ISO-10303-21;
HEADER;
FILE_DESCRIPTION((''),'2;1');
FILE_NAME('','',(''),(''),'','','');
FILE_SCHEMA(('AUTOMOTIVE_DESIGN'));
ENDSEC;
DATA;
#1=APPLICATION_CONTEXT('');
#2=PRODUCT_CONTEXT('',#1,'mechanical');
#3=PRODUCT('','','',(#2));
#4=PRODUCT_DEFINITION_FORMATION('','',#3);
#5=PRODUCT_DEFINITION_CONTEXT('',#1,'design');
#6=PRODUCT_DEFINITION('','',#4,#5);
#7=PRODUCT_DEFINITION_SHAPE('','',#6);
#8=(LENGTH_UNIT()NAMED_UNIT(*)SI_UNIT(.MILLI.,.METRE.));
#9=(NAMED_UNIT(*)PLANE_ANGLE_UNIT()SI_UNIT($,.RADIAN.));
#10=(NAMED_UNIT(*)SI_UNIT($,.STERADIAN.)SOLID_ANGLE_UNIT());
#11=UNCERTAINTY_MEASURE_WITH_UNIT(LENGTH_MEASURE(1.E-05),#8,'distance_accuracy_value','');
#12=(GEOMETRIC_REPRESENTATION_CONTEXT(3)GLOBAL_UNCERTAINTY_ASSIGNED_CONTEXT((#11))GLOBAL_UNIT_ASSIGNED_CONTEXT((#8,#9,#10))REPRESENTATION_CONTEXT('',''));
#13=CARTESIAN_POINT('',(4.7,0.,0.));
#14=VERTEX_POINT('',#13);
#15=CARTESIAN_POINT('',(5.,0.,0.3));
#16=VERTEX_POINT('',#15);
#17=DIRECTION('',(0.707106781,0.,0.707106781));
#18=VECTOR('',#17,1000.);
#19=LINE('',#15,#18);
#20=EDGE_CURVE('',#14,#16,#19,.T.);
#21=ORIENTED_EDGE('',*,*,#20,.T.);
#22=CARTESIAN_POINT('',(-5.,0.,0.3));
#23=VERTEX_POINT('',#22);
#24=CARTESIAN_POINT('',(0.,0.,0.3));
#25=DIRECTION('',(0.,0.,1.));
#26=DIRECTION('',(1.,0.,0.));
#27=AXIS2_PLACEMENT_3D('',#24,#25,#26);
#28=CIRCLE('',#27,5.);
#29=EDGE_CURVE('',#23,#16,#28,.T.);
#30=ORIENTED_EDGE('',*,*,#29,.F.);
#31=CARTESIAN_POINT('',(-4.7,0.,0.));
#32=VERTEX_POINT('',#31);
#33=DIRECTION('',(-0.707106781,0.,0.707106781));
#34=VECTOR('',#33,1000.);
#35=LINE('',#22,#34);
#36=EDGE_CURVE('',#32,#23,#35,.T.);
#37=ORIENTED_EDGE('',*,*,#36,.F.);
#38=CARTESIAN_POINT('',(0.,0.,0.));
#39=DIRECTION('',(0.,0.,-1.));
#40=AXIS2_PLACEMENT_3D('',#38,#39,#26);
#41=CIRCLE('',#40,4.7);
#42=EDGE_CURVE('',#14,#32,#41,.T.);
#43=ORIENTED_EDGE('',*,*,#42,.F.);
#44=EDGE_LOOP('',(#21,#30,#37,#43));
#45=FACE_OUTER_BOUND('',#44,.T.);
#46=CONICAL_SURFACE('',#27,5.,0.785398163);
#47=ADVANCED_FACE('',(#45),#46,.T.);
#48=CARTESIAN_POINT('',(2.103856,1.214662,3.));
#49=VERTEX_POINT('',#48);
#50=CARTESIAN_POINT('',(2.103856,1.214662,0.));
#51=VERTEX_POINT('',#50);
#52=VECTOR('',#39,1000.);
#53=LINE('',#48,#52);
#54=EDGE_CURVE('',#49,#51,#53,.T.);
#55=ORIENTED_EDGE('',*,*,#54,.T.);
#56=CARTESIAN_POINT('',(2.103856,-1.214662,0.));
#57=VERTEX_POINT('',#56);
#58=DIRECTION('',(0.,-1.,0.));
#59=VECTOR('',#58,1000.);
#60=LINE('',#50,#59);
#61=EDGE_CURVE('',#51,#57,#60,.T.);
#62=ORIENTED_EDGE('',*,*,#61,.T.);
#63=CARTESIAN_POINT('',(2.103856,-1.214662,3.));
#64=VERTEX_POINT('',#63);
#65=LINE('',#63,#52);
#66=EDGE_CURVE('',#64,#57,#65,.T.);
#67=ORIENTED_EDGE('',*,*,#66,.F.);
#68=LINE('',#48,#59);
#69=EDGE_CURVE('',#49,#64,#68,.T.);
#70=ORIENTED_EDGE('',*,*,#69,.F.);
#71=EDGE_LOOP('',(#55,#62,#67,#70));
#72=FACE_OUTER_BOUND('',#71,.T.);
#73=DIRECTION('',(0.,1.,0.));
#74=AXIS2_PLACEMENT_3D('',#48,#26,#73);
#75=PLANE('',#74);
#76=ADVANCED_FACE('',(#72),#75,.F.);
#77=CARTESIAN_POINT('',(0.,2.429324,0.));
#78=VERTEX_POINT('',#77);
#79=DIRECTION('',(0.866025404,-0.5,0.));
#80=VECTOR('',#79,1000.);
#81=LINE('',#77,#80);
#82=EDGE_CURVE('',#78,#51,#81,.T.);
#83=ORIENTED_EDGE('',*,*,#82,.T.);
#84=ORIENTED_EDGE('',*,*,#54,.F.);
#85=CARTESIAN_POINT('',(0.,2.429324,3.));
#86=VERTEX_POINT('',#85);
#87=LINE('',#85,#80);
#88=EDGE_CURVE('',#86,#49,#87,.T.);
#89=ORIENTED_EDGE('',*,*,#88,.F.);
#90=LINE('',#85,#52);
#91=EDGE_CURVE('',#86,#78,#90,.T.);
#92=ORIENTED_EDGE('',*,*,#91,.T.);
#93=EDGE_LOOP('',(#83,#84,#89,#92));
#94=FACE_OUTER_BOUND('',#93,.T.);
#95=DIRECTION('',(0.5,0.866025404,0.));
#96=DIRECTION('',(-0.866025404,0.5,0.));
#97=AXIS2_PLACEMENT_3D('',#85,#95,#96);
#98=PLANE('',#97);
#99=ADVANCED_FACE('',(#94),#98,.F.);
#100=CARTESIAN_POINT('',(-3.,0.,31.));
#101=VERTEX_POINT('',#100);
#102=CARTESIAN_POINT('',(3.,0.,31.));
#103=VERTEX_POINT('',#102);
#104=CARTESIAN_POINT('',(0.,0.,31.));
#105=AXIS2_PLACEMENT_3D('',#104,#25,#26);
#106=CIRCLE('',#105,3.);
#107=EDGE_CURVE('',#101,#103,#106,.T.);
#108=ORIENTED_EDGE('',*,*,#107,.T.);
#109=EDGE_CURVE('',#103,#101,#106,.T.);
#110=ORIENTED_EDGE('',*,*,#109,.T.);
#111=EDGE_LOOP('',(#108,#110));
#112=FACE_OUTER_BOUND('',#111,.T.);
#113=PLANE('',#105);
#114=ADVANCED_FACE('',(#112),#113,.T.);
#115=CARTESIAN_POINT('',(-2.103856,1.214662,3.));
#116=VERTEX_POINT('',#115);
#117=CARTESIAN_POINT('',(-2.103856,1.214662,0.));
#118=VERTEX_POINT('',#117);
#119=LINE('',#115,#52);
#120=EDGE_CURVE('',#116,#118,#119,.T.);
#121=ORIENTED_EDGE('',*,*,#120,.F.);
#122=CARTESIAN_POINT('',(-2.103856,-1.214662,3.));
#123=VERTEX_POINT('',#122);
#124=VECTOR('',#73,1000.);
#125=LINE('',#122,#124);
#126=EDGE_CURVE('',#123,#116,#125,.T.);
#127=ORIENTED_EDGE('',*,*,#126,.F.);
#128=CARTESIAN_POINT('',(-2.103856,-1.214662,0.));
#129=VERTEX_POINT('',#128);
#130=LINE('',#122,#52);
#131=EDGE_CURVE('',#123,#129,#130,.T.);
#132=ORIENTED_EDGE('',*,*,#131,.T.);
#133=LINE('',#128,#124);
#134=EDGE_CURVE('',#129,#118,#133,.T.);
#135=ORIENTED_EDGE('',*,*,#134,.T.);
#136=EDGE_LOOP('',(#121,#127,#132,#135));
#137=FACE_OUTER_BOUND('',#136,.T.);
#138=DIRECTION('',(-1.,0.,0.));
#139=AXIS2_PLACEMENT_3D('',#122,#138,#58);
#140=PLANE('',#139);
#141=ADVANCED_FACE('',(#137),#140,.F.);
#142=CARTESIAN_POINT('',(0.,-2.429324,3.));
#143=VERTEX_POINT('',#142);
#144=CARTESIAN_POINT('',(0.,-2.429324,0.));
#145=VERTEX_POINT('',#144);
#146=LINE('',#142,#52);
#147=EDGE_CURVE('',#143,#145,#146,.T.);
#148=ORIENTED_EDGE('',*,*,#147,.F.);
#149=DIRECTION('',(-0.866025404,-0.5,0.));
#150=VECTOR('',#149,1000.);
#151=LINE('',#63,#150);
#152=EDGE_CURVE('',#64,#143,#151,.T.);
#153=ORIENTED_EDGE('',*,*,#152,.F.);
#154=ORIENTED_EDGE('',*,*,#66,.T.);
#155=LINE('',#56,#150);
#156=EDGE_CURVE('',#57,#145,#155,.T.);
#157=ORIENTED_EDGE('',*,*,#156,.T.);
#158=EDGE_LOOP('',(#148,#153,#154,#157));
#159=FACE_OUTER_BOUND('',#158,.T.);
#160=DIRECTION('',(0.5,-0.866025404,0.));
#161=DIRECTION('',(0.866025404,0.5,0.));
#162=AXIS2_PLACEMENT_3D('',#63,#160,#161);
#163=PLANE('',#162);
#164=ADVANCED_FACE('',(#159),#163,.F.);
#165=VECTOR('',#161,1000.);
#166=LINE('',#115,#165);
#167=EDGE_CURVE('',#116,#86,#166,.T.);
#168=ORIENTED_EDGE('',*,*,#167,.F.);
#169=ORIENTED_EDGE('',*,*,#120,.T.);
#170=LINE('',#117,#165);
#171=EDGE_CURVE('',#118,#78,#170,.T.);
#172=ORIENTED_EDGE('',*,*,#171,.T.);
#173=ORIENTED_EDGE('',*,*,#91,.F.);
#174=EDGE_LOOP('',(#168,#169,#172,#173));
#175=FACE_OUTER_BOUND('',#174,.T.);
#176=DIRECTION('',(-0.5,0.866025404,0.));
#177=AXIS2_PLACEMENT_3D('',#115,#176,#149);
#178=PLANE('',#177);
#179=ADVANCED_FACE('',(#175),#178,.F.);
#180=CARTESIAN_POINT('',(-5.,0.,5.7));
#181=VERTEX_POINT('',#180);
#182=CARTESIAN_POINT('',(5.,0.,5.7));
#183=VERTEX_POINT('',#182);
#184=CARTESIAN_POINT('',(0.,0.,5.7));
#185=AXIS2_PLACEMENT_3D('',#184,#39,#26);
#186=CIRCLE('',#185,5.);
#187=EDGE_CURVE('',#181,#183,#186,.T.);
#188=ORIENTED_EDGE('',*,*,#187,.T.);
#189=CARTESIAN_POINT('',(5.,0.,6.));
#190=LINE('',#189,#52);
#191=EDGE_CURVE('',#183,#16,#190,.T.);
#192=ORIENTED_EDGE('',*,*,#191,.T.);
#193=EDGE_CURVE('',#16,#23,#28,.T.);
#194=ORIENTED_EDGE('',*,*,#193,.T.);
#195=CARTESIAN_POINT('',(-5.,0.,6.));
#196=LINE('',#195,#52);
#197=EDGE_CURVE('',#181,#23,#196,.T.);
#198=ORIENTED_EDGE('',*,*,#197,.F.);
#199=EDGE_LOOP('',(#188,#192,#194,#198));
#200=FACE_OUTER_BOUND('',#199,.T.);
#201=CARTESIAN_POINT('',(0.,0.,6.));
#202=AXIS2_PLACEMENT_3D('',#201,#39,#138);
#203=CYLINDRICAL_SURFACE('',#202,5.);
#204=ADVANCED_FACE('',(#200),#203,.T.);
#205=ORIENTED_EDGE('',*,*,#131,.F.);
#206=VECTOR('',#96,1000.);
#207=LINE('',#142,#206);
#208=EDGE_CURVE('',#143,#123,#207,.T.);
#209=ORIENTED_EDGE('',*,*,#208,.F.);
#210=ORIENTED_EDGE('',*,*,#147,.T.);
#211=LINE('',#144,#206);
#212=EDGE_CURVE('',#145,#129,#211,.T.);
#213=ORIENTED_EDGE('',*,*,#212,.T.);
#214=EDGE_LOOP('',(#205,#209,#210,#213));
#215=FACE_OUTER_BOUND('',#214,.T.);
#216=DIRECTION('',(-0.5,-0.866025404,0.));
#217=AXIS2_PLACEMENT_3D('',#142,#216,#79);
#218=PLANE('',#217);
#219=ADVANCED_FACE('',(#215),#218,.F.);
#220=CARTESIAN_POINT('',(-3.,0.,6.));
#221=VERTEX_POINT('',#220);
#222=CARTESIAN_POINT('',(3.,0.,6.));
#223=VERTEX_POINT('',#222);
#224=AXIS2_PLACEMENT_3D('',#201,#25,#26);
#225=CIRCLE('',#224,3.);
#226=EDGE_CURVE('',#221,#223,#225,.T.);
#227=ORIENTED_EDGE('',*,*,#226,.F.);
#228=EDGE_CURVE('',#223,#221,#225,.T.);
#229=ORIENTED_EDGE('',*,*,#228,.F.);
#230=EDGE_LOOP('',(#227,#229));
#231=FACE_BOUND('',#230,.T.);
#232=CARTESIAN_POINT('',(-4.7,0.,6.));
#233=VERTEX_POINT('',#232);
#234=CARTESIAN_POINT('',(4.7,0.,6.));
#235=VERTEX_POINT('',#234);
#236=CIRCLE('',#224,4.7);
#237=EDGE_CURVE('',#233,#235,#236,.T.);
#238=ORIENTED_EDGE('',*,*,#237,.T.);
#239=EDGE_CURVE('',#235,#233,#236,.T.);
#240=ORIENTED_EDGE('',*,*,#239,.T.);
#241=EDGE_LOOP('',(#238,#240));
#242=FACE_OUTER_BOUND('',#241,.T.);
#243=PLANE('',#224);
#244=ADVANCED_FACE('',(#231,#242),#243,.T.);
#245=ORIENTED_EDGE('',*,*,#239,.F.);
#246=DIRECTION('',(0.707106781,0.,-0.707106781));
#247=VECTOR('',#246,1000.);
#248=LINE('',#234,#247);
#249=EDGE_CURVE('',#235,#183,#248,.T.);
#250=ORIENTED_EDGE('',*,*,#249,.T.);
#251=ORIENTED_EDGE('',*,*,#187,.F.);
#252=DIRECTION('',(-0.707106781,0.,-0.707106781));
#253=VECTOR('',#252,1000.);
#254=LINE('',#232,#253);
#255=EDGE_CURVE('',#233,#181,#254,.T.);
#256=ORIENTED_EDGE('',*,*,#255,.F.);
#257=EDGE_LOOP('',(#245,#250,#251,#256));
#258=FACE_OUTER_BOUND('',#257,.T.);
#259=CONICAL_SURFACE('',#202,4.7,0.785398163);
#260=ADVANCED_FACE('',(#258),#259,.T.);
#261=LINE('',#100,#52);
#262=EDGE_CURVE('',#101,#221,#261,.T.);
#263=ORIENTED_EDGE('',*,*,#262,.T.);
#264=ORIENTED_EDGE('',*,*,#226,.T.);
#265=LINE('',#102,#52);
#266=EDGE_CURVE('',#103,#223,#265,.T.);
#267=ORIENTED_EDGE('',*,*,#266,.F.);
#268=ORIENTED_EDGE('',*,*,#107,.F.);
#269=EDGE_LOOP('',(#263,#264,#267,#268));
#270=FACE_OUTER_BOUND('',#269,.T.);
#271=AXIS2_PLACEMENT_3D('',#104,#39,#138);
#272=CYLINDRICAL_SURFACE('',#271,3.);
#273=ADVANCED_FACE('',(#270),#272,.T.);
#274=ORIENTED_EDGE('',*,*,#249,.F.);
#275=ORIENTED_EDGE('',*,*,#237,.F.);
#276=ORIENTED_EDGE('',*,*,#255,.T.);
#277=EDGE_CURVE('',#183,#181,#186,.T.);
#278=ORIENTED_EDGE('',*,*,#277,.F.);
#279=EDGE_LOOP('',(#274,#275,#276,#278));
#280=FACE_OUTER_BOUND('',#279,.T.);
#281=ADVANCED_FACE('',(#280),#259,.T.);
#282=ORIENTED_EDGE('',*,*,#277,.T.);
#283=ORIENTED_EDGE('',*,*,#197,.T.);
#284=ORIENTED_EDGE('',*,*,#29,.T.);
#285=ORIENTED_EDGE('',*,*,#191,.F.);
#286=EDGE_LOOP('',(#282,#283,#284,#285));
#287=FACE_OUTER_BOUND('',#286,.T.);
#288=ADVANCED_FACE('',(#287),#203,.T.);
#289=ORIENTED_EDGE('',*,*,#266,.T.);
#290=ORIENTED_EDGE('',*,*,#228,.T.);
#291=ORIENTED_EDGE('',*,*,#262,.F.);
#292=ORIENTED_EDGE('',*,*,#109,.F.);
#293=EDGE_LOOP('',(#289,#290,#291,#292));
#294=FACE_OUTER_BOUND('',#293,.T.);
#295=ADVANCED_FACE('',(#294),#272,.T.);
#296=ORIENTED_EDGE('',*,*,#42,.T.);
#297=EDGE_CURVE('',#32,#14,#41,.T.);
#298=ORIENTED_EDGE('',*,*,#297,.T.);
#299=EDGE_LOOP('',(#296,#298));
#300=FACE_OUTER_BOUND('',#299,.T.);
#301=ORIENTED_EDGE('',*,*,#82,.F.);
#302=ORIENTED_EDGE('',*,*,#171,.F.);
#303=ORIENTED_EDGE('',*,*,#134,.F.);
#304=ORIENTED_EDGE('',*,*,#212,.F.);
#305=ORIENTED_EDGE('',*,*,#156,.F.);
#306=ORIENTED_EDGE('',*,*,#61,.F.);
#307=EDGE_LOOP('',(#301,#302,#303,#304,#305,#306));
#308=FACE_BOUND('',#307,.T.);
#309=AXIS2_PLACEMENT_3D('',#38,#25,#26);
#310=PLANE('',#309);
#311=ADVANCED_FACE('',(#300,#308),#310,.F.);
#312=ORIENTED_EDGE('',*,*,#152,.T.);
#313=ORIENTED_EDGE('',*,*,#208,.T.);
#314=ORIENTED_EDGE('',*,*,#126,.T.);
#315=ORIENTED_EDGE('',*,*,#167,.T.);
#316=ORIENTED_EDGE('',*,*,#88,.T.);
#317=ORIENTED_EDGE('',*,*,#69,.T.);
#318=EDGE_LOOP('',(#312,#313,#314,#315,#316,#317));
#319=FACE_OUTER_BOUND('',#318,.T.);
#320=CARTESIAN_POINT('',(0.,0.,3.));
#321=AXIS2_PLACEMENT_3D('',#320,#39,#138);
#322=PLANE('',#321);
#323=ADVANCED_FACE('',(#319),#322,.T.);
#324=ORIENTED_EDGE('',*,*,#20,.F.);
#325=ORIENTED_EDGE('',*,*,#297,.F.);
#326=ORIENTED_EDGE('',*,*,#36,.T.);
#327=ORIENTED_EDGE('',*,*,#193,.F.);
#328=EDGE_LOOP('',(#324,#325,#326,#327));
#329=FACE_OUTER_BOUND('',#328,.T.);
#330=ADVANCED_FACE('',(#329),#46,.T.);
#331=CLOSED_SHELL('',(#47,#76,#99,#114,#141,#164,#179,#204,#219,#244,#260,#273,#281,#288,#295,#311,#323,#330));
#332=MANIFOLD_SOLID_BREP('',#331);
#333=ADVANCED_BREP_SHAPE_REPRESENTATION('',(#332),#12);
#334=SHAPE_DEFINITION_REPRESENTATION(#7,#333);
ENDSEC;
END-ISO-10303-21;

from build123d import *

# Parameters (mm, degrees)
SKETCH1_R           = 5
BOSS_EXTRUDE1_DEPTH = 6
SKETCH2_R           = 3
BOSS_EXTRUDE2_DEPTH = 25
CHAMFER1_SIZE       = 0.3
CUT_EXTRUDE1_DEPTH  = 3


with BuildPart() as part:
    # Sketch1 → Boss-Extrude1 (new body)
    with BuildSketch(Plane.XY):
        Circle(SKETCH1_R)
    extrude(amount=BOSS_EXTRUDE1_DEPTH)

    # Sketch2 → Boss-Extrude2 (add)
    with BuildSketch(Plane.XY.offset(6)):
        Circle(SKETCH2_R)
    extrude(amount=BOSS_EXTRUDE2_DEPTH)

    # Chamfer1
    chamfer1_edges = [part.edges().sort_by_distance(p)[0] for p in [
        (-5, 0, 0),
        (-5, 0, 6),
    ]]
    chamfer(chamfer1_edges, length=CHAMFER1_SIZE)

    # Sketch3 → Cut-Extrude1 (cut)
    with BuildSketch(Plane(origin=(0, 0, 0), x_dir=(-1, 0, 0), z_dir=(0, 0, -1))):
        Polygon((0, 2.42932406), (-2.10385635, 1.21466203), (-2.10385635, -1.21466203), (0, -2.42932406), (2.10385635, -1.21466203), (2.10385635, 1.21466203), align=None)
    extrude(amount=-CUT_EXTRUDE1_DEPTH, mode=Mode.SUBTRACT)


solid = part.part
